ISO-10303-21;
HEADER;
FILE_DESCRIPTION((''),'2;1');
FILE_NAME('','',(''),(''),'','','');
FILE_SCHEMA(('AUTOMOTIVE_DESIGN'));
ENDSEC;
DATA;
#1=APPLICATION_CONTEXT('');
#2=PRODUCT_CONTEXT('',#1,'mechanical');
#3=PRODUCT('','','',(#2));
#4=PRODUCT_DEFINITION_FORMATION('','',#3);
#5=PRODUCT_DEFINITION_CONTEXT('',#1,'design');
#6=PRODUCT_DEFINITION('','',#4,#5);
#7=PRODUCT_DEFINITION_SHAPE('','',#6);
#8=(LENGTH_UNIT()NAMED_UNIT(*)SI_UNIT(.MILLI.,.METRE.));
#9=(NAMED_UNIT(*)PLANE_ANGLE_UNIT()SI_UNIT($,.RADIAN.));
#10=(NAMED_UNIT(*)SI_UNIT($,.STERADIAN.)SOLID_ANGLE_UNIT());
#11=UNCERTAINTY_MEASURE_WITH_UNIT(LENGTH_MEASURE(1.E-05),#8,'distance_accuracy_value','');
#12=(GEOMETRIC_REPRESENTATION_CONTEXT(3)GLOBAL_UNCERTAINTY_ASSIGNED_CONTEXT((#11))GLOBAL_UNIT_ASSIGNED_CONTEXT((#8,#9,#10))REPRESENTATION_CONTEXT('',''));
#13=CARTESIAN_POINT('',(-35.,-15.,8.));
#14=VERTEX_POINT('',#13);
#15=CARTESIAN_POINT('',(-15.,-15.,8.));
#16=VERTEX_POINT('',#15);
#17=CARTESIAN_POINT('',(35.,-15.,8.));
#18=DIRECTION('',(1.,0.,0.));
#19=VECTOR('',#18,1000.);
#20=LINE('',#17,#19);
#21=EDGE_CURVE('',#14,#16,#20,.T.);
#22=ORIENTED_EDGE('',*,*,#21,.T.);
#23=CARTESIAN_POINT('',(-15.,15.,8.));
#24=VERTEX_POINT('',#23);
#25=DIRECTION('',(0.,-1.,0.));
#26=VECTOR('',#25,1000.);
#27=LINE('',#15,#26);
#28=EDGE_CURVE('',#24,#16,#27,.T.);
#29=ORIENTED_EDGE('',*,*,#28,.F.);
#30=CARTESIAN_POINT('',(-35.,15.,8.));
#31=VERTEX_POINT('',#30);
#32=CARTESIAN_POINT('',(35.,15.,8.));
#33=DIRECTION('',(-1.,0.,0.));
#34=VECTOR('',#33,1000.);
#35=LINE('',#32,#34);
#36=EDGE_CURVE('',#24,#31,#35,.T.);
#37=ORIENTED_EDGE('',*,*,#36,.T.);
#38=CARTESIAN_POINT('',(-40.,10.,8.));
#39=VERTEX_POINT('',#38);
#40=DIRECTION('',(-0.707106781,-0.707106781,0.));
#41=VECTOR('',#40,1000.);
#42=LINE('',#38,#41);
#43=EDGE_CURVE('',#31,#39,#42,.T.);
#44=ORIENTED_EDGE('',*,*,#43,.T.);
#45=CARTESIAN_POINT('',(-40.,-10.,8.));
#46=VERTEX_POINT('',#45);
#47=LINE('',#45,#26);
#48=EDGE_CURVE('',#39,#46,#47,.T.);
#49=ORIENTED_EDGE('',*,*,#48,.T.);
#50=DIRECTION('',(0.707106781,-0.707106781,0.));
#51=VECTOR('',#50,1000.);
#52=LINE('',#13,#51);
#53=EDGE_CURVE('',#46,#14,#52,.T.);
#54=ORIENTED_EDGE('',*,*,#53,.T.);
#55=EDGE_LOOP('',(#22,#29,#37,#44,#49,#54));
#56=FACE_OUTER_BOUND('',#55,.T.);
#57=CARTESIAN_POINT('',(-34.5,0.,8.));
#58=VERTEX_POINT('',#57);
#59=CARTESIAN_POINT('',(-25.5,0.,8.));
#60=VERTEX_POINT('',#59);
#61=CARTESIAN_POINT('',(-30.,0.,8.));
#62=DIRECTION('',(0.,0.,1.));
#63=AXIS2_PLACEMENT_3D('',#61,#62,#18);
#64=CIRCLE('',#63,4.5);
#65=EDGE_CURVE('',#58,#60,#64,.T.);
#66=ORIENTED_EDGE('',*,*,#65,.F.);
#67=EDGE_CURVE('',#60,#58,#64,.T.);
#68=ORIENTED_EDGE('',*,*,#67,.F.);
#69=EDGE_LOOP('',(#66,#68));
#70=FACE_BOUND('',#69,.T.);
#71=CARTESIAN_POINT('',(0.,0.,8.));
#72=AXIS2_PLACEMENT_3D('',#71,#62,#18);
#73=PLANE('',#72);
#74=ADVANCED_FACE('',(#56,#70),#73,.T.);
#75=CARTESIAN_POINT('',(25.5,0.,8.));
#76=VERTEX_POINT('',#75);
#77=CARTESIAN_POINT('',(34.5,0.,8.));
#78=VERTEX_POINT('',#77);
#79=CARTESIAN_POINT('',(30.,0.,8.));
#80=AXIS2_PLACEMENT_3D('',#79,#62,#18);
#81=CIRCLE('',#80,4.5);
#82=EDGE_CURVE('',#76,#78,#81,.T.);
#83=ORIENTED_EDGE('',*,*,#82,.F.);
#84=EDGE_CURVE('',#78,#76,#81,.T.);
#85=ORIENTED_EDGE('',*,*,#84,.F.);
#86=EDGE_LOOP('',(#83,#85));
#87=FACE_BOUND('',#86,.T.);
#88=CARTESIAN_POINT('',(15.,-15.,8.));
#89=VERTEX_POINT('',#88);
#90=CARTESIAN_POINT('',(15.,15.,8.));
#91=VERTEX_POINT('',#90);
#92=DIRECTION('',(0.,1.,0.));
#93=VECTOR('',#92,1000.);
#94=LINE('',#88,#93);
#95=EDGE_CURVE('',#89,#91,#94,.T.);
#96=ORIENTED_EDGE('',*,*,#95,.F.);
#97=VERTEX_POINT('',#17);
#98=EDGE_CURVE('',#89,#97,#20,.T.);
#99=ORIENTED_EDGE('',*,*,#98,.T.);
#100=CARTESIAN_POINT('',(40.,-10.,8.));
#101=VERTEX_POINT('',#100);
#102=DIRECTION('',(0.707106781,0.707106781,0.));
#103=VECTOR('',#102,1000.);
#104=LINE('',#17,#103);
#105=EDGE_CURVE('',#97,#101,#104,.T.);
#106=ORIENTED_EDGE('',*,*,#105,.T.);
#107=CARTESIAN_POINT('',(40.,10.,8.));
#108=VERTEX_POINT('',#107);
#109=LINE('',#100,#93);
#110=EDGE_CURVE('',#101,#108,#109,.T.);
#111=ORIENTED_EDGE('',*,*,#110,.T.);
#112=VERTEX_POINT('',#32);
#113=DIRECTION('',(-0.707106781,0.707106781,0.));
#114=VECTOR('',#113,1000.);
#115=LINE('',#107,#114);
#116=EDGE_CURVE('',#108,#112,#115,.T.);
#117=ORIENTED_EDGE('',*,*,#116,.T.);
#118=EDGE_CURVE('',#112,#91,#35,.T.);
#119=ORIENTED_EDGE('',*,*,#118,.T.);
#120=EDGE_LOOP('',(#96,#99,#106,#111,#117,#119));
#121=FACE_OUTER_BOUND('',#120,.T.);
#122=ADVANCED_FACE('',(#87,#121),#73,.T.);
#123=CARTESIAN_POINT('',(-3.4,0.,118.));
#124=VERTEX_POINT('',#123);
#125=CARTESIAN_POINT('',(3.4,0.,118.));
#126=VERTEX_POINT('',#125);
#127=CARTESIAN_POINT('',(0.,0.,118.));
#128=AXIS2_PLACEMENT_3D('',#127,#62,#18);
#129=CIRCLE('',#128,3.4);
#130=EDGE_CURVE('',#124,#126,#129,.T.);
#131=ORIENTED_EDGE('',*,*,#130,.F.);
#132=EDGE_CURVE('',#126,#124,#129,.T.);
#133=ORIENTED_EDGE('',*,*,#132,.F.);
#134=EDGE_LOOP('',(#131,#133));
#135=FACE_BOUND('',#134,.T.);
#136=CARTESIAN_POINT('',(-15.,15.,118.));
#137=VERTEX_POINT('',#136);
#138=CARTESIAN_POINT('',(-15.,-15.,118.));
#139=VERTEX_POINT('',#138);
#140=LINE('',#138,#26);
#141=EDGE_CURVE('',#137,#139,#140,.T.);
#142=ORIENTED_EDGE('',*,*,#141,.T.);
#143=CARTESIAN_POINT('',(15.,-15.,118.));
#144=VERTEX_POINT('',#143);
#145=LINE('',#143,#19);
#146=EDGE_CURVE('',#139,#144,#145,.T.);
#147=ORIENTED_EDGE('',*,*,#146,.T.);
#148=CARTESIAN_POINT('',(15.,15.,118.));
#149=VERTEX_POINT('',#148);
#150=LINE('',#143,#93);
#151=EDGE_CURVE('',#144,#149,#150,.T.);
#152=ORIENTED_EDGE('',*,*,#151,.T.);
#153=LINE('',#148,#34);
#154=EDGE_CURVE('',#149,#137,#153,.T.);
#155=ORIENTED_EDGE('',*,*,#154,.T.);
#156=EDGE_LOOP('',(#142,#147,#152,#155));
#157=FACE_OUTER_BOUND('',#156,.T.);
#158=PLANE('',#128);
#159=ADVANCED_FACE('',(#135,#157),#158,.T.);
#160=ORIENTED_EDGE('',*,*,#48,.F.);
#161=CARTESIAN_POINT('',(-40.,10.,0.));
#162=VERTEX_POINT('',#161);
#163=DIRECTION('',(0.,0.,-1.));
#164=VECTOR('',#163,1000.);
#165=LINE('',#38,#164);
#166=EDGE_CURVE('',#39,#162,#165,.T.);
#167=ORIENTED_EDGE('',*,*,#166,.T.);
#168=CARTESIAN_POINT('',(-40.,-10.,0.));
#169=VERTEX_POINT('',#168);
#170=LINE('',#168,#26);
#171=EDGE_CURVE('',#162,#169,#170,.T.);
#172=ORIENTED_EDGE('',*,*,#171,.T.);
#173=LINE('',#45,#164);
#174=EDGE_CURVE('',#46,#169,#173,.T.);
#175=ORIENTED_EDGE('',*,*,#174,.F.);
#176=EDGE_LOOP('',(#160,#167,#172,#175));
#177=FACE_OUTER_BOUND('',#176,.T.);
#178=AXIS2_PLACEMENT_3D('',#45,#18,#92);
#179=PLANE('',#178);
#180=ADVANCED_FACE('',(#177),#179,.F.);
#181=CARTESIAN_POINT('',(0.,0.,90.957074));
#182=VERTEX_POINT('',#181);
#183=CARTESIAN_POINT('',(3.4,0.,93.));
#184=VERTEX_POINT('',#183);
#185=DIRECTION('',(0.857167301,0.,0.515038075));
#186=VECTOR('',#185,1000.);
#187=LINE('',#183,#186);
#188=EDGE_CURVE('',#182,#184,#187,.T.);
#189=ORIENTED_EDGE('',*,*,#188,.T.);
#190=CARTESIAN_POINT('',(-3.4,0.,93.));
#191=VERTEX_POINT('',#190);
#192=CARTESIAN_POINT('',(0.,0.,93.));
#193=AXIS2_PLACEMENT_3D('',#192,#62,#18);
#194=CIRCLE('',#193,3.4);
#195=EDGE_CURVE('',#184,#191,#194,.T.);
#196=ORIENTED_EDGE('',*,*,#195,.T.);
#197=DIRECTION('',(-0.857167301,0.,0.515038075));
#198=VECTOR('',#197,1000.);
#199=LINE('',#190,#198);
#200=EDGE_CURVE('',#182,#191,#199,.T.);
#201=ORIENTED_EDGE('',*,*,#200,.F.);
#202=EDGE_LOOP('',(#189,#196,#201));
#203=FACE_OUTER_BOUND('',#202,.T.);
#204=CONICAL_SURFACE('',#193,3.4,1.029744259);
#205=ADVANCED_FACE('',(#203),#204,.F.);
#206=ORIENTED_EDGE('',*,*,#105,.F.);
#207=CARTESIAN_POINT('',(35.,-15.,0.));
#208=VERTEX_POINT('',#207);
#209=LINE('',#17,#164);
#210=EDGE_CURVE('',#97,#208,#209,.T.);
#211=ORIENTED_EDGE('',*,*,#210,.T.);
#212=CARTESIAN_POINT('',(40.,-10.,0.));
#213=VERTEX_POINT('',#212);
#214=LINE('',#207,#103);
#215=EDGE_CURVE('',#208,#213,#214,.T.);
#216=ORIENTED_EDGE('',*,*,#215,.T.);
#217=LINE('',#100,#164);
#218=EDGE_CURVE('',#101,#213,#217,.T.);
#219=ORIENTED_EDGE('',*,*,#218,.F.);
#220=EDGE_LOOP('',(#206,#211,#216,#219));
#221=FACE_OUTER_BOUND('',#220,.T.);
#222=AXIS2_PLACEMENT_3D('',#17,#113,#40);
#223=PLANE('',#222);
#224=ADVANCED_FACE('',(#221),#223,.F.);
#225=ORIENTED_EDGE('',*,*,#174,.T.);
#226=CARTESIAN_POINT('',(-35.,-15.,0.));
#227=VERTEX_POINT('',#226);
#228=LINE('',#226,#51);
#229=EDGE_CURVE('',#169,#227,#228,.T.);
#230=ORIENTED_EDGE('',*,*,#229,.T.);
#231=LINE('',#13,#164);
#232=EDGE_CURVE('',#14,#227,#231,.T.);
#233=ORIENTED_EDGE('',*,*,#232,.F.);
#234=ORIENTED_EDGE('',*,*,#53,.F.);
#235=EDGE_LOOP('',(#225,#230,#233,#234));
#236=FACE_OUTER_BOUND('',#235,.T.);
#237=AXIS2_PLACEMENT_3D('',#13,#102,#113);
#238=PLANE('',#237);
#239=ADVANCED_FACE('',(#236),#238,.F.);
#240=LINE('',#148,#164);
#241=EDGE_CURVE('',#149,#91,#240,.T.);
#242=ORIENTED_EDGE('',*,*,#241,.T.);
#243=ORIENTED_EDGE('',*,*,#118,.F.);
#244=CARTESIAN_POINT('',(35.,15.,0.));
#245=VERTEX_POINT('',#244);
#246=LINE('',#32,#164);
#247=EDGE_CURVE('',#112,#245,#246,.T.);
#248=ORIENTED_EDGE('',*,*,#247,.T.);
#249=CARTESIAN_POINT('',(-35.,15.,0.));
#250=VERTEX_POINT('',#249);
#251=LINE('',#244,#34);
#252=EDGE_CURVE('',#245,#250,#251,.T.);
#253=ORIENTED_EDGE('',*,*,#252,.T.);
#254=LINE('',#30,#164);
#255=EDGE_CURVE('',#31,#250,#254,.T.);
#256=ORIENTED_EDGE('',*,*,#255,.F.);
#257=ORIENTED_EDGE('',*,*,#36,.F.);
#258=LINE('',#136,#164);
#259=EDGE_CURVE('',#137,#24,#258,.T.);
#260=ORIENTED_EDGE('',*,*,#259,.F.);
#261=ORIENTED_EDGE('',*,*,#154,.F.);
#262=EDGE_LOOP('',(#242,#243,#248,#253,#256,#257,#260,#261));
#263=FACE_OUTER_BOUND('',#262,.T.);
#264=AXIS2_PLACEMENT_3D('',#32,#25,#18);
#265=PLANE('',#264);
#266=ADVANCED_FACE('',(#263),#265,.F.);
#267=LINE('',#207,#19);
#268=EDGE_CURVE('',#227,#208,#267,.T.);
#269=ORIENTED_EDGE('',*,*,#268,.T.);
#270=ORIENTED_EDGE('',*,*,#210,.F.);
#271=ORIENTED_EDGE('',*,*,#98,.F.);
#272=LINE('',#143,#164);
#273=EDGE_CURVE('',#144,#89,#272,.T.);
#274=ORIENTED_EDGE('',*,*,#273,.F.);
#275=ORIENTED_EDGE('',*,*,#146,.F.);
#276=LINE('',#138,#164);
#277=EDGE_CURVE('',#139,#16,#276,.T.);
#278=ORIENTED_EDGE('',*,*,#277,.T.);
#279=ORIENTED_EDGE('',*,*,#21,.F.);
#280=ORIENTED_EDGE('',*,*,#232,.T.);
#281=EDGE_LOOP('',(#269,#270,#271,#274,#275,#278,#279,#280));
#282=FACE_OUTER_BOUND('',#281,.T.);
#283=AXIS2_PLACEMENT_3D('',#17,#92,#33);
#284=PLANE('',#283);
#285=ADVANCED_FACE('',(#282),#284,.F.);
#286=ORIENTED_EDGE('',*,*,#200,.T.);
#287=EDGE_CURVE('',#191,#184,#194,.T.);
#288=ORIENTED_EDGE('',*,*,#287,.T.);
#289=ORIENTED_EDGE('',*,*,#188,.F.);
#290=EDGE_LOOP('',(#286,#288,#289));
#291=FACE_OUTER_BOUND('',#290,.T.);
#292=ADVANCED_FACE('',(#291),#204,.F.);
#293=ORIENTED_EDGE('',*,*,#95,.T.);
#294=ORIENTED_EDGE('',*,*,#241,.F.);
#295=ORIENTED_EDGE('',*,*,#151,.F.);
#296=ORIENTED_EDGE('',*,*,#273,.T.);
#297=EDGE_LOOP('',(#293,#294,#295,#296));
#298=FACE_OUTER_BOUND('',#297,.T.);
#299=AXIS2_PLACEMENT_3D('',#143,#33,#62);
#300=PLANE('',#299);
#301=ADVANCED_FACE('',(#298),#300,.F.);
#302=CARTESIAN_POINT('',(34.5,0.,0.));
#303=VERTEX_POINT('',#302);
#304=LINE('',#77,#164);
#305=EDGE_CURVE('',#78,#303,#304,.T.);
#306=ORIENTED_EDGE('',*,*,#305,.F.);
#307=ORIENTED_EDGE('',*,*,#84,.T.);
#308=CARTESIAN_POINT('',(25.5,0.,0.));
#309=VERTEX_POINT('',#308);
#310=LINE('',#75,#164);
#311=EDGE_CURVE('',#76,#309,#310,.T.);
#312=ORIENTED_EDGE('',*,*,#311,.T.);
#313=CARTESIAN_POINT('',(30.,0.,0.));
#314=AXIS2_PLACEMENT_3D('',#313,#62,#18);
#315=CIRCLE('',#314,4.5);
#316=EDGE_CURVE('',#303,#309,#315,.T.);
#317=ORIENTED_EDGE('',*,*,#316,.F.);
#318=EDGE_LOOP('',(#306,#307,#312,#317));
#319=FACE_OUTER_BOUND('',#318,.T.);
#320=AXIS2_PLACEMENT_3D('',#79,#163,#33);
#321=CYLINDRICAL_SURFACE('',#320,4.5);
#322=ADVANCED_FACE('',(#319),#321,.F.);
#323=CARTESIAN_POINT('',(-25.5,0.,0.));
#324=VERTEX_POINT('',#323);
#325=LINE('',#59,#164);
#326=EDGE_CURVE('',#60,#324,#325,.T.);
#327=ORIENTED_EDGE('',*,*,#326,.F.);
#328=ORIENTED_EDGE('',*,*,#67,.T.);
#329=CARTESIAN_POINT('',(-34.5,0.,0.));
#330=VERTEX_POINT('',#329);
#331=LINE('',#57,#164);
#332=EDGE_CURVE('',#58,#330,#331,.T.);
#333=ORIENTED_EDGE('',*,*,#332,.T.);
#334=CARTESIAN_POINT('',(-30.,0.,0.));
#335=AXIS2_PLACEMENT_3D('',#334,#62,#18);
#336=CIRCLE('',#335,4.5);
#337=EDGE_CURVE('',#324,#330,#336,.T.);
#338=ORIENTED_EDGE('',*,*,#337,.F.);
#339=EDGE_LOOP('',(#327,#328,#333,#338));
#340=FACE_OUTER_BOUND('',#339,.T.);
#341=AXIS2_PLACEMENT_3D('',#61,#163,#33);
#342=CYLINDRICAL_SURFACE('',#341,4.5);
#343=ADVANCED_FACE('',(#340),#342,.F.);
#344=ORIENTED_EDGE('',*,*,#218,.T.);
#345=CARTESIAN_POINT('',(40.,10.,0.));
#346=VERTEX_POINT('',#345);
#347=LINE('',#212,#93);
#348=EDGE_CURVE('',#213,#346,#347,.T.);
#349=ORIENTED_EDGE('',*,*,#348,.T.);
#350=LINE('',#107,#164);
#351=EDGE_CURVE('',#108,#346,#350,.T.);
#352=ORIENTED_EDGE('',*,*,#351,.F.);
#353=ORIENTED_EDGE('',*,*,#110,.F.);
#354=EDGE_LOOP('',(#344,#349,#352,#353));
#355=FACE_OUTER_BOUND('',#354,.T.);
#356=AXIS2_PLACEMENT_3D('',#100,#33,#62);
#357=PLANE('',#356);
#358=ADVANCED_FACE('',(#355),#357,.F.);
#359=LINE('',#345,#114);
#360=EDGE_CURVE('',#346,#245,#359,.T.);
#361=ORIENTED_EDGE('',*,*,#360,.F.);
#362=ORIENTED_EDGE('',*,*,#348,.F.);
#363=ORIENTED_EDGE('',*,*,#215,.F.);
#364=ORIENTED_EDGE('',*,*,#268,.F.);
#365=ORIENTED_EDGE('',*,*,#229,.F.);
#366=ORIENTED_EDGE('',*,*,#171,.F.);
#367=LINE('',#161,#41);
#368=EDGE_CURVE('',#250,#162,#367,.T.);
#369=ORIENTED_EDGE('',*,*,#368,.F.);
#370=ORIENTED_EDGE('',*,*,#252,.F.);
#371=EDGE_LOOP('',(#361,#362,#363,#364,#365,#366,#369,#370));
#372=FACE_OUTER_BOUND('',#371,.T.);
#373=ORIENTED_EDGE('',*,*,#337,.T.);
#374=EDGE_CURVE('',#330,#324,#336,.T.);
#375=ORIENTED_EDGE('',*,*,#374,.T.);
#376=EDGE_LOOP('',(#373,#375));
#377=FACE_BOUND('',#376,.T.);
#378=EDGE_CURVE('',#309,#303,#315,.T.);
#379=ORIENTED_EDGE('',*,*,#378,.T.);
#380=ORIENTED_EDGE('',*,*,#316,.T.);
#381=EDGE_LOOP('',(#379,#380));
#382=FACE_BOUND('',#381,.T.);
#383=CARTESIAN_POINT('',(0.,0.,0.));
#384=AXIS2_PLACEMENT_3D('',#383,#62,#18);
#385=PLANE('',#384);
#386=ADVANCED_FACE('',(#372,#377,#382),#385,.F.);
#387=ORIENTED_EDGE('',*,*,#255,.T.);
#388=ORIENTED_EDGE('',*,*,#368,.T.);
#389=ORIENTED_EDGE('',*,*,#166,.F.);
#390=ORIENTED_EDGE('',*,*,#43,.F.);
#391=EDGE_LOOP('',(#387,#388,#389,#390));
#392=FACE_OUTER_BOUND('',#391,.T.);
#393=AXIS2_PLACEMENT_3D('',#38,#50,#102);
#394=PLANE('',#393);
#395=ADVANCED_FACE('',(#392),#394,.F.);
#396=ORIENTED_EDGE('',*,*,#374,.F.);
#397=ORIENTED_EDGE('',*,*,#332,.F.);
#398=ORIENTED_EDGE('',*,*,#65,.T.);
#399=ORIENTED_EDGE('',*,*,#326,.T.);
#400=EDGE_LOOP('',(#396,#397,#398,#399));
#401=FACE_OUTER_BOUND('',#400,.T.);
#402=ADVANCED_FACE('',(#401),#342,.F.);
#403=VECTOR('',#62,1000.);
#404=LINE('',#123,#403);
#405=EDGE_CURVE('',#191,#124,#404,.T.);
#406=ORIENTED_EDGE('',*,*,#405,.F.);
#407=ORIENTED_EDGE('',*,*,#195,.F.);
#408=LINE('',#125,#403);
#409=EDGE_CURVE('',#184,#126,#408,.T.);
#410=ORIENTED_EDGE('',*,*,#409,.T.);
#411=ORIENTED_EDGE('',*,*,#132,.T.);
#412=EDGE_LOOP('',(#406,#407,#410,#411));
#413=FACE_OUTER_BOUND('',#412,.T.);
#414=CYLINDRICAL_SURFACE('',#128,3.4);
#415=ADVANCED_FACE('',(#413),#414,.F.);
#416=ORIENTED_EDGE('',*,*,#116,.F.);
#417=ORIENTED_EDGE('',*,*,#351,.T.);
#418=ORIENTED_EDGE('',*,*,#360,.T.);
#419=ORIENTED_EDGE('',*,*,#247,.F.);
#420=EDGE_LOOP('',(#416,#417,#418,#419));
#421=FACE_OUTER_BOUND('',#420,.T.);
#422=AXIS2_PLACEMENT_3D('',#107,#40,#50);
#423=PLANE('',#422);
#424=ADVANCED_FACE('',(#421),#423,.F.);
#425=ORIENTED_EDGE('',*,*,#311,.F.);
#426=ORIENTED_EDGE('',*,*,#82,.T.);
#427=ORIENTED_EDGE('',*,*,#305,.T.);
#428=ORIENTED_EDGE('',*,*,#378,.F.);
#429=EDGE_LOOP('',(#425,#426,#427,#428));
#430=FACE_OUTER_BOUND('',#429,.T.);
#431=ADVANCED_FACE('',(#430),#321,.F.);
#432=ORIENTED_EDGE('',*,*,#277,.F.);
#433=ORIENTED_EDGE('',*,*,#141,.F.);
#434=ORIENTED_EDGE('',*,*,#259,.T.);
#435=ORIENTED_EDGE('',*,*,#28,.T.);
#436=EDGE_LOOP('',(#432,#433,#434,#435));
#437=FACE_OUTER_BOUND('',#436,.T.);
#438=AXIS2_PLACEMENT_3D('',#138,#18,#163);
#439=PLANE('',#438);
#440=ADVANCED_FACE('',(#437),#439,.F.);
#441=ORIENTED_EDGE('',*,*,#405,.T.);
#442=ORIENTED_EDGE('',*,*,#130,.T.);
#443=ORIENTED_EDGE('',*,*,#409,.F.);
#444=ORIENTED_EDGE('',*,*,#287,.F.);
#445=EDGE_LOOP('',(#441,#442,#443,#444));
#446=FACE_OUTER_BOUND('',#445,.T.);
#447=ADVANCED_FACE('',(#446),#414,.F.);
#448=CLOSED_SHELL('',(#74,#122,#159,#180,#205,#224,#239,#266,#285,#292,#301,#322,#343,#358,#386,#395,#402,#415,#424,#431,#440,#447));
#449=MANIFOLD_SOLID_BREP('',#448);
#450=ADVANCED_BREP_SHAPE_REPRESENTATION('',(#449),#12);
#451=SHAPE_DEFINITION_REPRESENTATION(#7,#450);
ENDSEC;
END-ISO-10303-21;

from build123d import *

# Parameters (mm, degrees)
SKETCH1_R             = 4.5
BOSS_EXTRUDE1_DEPTH   = 8
SKETCH2_W             = 30
SKETCH2_H             = 30
BOSS_EXTRUDE2_DEPTH   = 110
SKETCH3_R             = 1.5
CUT_EXTRUDE1_DEPTH    = 10
M8_TAPPED_HOLE1_D     = 6.8
M8_TAPPED_HOLE1_DEPTH = 25
M8_TAPPED_HOLE1_TIP   = 2.042926105


with BuildPart() as part:
    # Sketch1 → Boss-Extrude1 (new body)
    with BuildSketch(Plane.XY):
        Polygon((-40, 10), (-35, 15), (35, 15), (40, 10), (40, -10), (35, -15), (-35, -15), (-40, -10), align=None)
        with Locations((-30, 0)):
            Circle(SKETCH1_R, mode=Mode.SUBTRACT)
        with Locations((30, 0)):
            Circle(SKETCH1_R, mode=Mode.SUBTRACT)
    extrude(amount=BOSS_EXTRUDE1_DEPTH)

    # Sketch2 → Boss-Extrude2 (add)
    with BuildSketch(Plane.XY.offset(8)):
        Rectangle(SKETCH2_W, SKETCH2_H)
    extrude(amount=BOSS_EXTRUDE2_DEPTH)

    # Sketch3 → Cut-Extrude1 (cut)
    with BuildSketch(Plane.XY.offset(118)):
        Circle(SKETCH3_R)
    extrude(amount=-CUT_EXTRUDE1_DEPTH, mode=Mode.SUBTRACT)

    # M8 Tapped Hole1
    with Locations(Plane.XY.offset(118)):
        with Locations((0, 0)):
            Hole(M8_TAPPED_HOLE1_D / 2, depth=M8_TAPPED_HOLE1_DEPTH)
            with Locations((0, 0, -(M8_TAPPED_HOLE1_DEPTH + M8_TAPPED_HOLE1_TIP / 2))):  # 118° drill point
                Cone(0, M8_TAPPED_HOLE1_D / 2, M8_TAPPED_HOLE1_TIP, mode=Mode.SUBTRACT)


solid = part.part
